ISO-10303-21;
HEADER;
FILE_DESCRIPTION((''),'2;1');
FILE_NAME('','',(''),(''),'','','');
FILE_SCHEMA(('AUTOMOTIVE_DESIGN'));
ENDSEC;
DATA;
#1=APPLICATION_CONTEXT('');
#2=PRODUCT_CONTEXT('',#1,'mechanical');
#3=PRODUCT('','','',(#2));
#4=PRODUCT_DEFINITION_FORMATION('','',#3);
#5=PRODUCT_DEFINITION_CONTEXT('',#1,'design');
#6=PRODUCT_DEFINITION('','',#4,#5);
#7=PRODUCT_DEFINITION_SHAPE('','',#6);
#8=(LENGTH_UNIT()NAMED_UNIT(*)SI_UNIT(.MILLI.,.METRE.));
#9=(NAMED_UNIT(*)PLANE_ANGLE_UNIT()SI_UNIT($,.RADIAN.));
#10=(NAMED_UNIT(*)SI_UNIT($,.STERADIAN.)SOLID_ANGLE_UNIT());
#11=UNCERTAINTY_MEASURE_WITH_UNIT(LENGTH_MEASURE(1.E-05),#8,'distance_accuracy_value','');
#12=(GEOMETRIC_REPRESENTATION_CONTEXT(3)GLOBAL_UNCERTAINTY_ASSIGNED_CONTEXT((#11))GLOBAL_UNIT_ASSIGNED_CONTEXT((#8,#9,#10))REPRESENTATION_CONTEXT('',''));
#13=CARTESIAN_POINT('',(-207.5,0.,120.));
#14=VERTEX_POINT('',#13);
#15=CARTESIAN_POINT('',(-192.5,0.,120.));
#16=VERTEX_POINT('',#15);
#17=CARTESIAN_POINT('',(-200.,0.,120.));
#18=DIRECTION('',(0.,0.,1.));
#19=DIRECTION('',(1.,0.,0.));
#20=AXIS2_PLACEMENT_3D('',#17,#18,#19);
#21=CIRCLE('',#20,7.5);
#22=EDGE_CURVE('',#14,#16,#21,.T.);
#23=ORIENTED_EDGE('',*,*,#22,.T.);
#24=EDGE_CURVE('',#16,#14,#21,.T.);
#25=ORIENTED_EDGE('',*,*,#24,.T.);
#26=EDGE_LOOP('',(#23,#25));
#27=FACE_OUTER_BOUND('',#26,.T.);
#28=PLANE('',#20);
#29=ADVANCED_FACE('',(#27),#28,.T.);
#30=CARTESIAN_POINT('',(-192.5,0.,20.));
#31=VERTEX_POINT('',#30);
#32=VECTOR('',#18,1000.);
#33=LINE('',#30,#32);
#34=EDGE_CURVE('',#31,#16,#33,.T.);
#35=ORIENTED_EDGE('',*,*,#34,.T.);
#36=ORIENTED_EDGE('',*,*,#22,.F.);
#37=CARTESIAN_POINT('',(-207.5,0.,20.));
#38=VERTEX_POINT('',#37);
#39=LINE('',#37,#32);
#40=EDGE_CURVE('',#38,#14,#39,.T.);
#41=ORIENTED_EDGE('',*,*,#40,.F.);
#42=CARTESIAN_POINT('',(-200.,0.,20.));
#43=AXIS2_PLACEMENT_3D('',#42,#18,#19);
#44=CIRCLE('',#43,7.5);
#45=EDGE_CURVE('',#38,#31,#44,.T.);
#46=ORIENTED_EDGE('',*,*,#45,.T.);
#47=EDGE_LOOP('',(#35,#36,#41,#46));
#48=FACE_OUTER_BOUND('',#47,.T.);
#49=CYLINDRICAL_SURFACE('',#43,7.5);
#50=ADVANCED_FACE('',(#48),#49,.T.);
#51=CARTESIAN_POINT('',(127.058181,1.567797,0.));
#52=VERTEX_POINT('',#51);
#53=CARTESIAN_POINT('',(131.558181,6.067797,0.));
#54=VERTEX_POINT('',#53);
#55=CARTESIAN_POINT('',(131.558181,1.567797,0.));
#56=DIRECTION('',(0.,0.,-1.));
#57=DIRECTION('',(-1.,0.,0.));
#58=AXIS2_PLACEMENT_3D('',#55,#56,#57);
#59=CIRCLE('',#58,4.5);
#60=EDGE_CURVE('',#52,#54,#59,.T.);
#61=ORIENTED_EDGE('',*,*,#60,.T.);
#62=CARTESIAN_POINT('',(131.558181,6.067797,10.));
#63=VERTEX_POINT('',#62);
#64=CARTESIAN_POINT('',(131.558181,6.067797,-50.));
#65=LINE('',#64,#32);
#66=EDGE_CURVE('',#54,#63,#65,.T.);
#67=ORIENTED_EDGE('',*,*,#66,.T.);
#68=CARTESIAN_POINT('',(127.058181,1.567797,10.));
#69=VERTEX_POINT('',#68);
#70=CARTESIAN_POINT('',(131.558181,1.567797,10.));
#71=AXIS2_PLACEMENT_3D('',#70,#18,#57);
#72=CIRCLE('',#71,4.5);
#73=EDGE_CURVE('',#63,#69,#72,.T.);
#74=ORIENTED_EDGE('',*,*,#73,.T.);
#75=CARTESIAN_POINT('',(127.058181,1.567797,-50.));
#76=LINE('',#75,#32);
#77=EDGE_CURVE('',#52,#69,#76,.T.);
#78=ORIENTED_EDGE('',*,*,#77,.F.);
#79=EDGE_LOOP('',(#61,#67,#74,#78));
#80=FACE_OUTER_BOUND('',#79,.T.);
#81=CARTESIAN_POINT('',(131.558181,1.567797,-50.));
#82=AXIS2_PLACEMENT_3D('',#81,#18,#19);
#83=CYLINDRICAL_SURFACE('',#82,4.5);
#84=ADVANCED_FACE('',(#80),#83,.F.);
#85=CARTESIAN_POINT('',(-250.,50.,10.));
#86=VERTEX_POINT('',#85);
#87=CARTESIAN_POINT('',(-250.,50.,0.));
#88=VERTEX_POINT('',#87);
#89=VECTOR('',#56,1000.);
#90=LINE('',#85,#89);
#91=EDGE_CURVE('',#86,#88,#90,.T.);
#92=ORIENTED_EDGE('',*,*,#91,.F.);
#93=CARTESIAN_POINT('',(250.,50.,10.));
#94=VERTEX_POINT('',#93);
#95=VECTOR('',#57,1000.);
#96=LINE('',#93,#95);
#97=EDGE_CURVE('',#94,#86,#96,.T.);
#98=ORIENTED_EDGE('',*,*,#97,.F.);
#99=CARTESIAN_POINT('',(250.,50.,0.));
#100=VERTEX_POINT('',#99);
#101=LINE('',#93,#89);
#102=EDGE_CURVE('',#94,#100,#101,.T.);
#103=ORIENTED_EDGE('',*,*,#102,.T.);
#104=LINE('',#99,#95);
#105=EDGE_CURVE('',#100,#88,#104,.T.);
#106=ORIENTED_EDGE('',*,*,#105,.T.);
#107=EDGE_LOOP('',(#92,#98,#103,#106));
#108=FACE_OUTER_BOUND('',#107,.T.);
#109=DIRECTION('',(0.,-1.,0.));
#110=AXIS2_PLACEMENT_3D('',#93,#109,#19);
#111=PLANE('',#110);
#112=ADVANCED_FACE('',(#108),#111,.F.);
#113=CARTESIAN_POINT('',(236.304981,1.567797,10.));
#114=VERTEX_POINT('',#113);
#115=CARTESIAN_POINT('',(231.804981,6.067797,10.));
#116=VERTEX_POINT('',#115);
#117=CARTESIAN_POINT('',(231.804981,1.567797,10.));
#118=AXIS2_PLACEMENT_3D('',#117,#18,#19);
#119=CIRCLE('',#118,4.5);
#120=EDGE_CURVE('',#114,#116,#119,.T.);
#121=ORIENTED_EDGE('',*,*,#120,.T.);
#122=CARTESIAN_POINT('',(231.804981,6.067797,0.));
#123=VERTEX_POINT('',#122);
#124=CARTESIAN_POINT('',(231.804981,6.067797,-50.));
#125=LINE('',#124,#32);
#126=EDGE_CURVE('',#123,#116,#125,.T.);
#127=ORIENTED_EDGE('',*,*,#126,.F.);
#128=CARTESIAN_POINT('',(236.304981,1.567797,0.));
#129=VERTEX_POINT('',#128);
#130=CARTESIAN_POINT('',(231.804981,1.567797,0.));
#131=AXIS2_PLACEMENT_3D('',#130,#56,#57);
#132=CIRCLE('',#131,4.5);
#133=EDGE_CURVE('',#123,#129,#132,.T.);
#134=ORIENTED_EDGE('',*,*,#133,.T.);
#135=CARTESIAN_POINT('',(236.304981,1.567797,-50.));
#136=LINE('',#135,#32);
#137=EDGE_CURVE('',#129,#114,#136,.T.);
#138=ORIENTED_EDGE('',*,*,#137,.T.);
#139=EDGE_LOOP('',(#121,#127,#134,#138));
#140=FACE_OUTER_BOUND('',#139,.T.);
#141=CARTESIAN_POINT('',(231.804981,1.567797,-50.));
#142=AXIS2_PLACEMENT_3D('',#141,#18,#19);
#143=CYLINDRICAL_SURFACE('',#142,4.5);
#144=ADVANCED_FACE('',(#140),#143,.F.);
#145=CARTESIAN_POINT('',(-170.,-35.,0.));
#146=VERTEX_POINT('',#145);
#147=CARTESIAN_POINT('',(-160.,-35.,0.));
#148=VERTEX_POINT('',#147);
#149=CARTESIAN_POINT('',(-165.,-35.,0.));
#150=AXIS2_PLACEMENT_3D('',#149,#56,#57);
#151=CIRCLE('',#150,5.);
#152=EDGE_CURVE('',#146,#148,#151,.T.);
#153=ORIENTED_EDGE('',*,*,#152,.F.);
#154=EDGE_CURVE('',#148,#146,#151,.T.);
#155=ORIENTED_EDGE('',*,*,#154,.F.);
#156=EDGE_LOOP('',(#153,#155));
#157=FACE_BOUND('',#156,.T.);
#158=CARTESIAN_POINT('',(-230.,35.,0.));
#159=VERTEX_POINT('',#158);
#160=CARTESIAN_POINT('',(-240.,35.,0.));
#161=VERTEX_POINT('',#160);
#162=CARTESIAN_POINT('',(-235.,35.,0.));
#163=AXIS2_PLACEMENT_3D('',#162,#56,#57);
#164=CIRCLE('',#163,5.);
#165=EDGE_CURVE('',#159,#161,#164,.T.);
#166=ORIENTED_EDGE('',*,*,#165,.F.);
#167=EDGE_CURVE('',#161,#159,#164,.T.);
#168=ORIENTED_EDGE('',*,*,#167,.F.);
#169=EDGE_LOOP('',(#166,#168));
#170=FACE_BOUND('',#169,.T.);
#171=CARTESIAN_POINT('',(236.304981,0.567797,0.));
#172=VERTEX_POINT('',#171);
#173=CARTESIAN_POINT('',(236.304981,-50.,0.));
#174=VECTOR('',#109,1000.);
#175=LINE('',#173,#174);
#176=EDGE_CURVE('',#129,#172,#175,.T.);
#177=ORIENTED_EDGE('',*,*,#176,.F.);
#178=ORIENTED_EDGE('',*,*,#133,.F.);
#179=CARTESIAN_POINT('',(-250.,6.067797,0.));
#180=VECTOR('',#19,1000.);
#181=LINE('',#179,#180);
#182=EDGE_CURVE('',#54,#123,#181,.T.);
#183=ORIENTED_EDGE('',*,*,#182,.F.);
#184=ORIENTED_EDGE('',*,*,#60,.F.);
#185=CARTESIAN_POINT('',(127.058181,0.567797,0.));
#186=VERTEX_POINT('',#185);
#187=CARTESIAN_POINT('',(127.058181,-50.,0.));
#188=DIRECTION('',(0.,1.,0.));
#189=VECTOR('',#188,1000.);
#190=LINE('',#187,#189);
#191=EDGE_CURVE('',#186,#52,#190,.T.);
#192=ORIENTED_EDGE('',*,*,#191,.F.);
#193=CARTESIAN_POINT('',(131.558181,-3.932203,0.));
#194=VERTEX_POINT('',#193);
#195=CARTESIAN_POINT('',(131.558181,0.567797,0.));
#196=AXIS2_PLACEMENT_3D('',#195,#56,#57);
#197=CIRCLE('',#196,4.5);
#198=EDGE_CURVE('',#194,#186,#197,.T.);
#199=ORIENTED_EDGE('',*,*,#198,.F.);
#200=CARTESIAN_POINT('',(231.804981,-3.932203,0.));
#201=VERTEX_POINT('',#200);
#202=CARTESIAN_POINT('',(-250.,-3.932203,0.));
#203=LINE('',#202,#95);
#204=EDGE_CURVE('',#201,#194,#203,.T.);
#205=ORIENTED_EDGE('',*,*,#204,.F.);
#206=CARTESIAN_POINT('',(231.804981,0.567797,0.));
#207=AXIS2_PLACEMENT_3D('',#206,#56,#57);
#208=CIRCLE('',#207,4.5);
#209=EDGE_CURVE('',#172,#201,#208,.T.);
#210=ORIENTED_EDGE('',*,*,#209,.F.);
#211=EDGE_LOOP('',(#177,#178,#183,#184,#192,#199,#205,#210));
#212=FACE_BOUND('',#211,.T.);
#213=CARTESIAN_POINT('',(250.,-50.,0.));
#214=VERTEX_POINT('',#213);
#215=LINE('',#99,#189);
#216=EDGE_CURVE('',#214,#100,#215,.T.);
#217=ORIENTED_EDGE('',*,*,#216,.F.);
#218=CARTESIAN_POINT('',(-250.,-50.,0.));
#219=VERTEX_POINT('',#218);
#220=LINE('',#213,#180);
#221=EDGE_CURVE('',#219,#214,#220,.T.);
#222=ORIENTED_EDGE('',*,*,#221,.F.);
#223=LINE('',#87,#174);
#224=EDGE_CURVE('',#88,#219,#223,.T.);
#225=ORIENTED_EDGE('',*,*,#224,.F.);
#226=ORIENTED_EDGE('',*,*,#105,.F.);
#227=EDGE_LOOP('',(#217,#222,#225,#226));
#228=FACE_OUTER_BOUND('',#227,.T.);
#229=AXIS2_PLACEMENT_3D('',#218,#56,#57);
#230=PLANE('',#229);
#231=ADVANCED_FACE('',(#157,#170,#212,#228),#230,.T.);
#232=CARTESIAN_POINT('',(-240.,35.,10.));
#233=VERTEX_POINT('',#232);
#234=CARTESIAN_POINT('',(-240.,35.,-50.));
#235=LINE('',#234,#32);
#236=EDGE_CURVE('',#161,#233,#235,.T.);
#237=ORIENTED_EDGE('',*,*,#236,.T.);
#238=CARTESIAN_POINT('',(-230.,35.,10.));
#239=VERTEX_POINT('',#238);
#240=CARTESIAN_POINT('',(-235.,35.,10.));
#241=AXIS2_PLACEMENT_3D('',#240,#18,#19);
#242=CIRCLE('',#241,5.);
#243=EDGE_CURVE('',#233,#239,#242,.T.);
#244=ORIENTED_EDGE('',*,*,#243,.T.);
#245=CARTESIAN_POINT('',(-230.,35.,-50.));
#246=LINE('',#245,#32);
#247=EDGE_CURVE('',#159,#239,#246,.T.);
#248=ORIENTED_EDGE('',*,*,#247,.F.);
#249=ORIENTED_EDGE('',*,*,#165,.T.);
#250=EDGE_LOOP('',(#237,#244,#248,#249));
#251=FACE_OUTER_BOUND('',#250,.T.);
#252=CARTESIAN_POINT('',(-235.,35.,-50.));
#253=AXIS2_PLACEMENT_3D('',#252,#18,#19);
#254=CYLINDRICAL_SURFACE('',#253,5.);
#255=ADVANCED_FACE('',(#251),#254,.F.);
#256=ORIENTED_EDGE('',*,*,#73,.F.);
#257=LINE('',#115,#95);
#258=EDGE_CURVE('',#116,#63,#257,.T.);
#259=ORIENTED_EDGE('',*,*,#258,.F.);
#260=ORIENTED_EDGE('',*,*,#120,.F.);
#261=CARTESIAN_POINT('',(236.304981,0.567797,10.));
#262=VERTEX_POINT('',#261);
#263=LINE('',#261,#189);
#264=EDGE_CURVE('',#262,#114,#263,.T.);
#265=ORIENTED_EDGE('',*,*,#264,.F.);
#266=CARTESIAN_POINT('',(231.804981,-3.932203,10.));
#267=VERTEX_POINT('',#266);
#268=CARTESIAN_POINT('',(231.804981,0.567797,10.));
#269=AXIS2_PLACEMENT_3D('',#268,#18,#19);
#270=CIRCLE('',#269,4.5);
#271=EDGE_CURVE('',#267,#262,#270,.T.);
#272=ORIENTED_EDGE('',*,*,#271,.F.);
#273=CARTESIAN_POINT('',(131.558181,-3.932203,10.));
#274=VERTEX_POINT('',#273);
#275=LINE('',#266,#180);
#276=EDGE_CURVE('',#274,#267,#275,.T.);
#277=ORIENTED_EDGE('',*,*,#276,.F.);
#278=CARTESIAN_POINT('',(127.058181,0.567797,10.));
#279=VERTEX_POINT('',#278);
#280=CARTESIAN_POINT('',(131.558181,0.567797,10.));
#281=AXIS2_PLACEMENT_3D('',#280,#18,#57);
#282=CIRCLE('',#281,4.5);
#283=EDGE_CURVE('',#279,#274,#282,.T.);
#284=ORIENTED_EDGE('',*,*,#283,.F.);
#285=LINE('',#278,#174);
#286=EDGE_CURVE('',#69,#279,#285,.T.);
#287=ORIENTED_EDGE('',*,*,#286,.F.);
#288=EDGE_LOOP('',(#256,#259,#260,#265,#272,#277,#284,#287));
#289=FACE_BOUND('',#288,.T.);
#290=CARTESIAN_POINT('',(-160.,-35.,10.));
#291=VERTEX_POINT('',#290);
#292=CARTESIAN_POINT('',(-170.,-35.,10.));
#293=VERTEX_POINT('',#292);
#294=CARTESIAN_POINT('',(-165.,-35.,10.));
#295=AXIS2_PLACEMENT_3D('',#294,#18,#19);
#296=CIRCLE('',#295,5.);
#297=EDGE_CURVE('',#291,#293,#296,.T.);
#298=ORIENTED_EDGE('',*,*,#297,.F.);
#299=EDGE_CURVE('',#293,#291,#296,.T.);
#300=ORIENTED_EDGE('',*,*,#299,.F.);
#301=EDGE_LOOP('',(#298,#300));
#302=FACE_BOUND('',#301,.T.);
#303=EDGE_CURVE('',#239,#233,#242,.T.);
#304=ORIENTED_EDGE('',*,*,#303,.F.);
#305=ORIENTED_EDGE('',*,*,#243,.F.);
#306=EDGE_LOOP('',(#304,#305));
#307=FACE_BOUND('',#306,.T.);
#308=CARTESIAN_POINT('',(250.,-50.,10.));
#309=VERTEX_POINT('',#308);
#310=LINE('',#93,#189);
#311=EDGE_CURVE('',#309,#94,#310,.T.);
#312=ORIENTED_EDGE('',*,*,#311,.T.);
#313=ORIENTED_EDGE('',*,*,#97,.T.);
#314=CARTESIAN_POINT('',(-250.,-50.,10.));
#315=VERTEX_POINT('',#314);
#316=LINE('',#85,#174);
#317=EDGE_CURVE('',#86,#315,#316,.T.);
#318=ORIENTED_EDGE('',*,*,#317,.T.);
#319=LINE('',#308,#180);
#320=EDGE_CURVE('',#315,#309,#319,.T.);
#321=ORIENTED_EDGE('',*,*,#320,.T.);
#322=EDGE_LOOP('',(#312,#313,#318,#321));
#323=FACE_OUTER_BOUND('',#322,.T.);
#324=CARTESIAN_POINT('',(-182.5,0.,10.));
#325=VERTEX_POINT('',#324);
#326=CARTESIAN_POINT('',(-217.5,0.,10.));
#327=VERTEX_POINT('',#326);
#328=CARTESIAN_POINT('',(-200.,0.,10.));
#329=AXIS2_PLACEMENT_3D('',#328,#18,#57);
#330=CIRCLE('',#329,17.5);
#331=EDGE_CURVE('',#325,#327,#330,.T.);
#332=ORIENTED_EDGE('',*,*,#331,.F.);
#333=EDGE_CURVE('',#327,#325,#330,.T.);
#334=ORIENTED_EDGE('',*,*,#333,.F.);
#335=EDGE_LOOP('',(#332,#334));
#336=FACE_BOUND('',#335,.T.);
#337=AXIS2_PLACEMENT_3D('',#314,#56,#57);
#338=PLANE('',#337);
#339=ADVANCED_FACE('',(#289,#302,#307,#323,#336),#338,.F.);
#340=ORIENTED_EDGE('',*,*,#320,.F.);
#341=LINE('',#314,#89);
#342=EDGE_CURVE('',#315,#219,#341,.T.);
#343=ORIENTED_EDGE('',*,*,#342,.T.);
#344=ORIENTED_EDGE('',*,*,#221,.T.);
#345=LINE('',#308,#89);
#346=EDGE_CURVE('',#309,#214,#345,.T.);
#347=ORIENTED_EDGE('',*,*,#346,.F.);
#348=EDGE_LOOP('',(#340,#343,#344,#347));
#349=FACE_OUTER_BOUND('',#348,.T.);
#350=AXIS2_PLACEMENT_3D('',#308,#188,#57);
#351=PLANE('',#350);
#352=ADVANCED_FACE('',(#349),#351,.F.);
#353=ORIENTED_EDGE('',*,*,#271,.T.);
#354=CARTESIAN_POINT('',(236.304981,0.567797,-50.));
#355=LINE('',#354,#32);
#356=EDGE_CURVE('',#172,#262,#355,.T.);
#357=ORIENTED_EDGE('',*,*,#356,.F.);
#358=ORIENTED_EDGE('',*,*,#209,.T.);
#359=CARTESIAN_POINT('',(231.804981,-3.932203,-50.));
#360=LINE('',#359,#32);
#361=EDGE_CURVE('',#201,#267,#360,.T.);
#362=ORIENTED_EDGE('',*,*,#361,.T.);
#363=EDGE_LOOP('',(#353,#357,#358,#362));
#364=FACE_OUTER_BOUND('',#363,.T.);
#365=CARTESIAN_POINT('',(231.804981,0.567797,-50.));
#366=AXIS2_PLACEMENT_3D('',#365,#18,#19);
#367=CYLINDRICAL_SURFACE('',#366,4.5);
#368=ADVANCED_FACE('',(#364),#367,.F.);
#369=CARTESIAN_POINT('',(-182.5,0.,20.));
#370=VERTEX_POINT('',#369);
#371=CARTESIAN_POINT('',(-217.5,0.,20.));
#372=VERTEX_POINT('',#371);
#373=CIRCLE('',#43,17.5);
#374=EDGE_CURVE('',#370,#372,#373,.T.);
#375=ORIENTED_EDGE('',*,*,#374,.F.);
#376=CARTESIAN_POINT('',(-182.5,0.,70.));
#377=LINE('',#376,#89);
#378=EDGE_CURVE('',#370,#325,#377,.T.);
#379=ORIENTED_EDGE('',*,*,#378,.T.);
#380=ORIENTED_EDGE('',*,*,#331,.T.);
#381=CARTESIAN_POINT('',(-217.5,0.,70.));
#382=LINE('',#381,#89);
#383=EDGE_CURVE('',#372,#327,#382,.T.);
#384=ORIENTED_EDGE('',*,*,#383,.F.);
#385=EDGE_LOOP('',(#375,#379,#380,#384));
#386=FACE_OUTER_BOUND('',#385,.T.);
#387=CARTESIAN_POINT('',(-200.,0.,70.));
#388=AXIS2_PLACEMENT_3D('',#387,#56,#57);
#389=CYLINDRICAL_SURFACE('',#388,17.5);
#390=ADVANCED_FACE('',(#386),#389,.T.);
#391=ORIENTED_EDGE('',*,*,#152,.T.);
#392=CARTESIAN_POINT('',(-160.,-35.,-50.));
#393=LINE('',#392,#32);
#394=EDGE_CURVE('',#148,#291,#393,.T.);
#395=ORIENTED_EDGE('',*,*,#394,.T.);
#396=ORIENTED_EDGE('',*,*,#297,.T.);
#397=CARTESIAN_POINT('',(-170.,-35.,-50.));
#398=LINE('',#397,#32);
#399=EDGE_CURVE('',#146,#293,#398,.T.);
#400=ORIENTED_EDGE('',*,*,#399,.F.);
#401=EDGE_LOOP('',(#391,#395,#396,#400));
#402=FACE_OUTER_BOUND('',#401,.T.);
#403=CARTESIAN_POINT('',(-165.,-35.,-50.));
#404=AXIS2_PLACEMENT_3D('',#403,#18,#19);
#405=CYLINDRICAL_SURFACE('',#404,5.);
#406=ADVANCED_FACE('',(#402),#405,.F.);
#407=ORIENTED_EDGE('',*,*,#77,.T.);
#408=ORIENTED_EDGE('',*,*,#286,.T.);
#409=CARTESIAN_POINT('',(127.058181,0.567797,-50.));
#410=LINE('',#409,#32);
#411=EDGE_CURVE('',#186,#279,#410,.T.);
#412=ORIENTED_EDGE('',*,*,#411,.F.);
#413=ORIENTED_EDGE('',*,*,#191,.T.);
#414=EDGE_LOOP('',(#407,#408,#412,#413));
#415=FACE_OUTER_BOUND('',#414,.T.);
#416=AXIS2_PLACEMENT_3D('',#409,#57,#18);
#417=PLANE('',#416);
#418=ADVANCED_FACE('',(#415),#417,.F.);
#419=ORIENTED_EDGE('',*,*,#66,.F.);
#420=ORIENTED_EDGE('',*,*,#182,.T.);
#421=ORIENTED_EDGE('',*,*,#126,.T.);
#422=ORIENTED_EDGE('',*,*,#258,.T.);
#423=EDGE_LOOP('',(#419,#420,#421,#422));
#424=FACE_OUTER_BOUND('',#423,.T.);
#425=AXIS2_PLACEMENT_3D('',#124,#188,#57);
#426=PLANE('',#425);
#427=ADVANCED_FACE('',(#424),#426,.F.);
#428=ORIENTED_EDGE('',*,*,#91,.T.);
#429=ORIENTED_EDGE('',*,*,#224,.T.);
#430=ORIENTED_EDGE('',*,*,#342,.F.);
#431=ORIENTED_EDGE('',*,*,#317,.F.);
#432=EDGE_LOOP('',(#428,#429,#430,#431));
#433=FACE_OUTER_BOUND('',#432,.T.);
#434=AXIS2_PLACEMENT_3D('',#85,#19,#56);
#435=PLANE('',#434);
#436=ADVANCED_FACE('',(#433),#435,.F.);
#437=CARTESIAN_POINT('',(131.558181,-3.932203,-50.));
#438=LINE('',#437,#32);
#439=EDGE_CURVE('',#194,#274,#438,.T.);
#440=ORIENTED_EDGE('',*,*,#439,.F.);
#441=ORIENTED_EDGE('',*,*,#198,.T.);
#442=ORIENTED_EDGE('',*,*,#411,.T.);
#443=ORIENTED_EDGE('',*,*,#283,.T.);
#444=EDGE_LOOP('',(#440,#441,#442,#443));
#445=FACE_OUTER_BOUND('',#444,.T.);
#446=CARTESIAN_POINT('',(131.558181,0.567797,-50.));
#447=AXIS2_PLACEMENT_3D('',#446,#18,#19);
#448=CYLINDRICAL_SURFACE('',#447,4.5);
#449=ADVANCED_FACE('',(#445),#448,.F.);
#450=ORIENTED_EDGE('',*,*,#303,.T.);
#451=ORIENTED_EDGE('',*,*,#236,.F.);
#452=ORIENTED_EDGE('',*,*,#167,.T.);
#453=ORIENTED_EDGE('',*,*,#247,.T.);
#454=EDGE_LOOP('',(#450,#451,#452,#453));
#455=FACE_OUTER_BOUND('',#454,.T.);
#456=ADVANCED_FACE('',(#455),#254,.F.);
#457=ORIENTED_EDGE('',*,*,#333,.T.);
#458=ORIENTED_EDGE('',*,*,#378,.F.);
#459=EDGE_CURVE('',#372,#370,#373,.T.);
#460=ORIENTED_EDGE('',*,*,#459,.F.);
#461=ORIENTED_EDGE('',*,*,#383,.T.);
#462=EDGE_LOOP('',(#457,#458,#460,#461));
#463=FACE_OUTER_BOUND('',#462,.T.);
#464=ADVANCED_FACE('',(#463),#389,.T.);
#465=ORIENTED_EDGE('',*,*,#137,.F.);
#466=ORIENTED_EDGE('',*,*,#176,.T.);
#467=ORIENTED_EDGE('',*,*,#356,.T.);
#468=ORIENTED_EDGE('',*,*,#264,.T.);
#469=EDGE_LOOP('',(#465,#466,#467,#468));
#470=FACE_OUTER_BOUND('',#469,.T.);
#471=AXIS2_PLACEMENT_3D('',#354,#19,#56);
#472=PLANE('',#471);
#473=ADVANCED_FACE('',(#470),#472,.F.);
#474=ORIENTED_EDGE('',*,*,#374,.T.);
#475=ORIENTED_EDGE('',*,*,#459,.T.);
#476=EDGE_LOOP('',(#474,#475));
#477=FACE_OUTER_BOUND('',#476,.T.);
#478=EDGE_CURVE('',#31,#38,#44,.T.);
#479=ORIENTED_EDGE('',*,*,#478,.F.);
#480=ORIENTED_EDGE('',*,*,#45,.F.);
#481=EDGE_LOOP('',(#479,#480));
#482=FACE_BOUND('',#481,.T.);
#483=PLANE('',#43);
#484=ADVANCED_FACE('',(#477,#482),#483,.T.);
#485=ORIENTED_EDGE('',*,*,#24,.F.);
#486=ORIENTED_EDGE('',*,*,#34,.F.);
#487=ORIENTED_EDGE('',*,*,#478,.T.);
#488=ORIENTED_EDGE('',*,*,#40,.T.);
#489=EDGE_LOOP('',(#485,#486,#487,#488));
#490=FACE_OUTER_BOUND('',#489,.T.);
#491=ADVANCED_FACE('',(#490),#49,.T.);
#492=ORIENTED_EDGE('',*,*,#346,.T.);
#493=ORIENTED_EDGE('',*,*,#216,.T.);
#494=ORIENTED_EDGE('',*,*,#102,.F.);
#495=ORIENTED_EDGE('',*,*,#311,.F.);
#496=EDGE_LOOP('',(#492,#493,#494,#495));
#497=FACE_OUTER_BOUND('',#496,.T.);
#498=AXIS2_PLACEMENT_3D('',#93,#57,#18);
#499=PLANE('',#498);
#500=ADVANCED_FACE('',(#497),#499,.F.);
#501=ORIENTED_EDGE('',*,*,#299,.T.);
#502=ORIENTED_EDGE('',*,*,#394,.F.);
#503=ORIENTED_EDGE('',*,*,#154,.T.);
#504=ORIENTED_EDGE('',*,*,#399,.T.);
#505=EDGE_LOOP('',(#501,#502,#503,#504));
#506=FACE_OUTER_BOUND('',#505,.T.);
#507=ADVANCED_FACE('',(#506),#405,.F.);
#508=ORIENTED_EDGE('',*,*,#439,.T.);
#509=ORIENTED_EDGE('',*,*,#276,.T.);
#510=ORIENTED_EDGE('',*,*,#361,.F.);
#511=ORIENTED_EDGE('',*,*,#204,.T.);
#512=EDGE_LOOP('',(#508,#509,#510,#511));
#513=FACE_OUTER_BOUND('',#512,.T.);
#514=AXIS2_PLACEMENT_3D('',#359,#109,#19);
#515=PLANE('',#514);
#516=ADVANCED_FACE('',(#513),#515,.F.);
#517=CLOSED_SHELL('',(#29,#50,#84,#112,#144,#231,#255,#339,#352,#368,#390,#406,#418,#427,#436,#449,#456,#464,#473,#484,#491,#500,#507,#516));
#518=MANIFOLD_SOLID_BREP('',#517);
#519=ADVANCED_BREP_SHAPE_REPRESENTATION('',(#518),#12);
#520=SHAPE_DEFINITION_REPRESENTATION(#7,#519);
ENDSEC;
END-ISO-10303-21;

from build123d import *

# Parameters (mm, degrees)
SKETCH1_W           = 500
SKETCH1_H           = 100
BOSS_EXTRUDE1_DEPTH = 10
CUT_EXTRUDE1_DEPTH  = 60
SKETCH4_R           = 5
CUT_EXTRUDE2_DEPTH  = 60
SKETCH2_R           = 17.5
BOSS_EXTRUDE2_DEPTH = 60
CUT_EXTRUDE3_START  = -50
SKETCH5_R           = 17.5
SKETCH5_R_2         = 7.5
CUT_EXTRUDE3_DEPTH  = 50
SKETCH6_R           = 7.5
BOSS_EXTRUDE3_DEPTH = 50


with BuildPart() as part:
    # Sketch1 → Boss-Extrude1 (new body)
    with BuildSketch(Plane.XY):
        Rectangle(SKETCH1_W, SKETCH1_H)
    extrude(amount=BOSS_EXTRUDE1_DEPTH)

    # Sketch3 → Cut-Extrude1 (cut)
    with BuildSketch(Plane.XY.offset(10)):
        with BuildLine():
            Line((231.804981109, -3.932202525), (131.558181165, -3.932202525))
            ThreePointArc((131.558181165, -3.932202525), (128.376200649, -2.614183041), (127.058181165, 0.567797475))
            Line((127.058181165, 0.567797475), (127.058181165, 1.567797475))
            ThreePointArc((127.058181165, 1.567797475), (128.376200649, 4.74977799), (131.558181165, 6.067797475))
            Line((131.558181165, 6.067797475), (231.804981109, 6.067797475))
            ThreePointArc((231.804981109, 6.067797475), (234.986961624, 4.74977799), (236.304981109, 1.567797475))
            Line((236.304981109, 1.567797475), (236.304981109, 0.567797475))
            ThreePointArc((236.304981109, 0.567797475), (234.986961624, -2.614183041), (231.804981109, -3.932202525))
        make_face()
    extrude(amount=-CUT_EXTRUDE1_DEPTH, mode=Mode.SUBTRACT)

    # Sketch4 → Cut-Extrude2 (cut)
    with BuildSketch(Plane.XY.offset(10)):
        with Locations((-235, 35)):
            Circle(SKETCH4_R)
        with Locations((-165, -35)):
            Circle(SKETCH4_R)
    extrude(amount=-CUT_EXTRUDE2_DEPTH, mode=Mode.SUBTRACT)

    # Sketch2 → Boss-Extrude2 (add)
    with BuildSketch(Plane.XY.offset(10)):
        with Locations(Location((-200, 0, 0), (0, 0, 180))):
            Circle(SKETCH2_R)
    extrude(amount=BOSS_EXTRUDE2_DEPTH)

    # Sketch5 → Cut-Extrude3 (cut)
    with BuildSketch(Plane.XY.offset(70).offset(CUT_EXTRUDE3_START)):
        with Locations(Location((-200, 0, 0), (0, 0, 180))):
            Circle(SKETCH5_R)
        with Locations((-200, 0)):
            Circle(SKETCH5_R_2, mode=Mode.SUBTRACT)
    extrude(amount=CUT_EXTRUDE3_DEPTH, mode=Mode.SUBTRACT)

    # Sketch6 → Boss-Extrude3 (add)
    with BuildSketch(Plane.XY.offset(70)):
        with Locations((-200, 0)):
            Circle(SKETCH6_R)
    extrude(amount=BOSS_EXTRUDE3_DEPTH)


solid = part.part
